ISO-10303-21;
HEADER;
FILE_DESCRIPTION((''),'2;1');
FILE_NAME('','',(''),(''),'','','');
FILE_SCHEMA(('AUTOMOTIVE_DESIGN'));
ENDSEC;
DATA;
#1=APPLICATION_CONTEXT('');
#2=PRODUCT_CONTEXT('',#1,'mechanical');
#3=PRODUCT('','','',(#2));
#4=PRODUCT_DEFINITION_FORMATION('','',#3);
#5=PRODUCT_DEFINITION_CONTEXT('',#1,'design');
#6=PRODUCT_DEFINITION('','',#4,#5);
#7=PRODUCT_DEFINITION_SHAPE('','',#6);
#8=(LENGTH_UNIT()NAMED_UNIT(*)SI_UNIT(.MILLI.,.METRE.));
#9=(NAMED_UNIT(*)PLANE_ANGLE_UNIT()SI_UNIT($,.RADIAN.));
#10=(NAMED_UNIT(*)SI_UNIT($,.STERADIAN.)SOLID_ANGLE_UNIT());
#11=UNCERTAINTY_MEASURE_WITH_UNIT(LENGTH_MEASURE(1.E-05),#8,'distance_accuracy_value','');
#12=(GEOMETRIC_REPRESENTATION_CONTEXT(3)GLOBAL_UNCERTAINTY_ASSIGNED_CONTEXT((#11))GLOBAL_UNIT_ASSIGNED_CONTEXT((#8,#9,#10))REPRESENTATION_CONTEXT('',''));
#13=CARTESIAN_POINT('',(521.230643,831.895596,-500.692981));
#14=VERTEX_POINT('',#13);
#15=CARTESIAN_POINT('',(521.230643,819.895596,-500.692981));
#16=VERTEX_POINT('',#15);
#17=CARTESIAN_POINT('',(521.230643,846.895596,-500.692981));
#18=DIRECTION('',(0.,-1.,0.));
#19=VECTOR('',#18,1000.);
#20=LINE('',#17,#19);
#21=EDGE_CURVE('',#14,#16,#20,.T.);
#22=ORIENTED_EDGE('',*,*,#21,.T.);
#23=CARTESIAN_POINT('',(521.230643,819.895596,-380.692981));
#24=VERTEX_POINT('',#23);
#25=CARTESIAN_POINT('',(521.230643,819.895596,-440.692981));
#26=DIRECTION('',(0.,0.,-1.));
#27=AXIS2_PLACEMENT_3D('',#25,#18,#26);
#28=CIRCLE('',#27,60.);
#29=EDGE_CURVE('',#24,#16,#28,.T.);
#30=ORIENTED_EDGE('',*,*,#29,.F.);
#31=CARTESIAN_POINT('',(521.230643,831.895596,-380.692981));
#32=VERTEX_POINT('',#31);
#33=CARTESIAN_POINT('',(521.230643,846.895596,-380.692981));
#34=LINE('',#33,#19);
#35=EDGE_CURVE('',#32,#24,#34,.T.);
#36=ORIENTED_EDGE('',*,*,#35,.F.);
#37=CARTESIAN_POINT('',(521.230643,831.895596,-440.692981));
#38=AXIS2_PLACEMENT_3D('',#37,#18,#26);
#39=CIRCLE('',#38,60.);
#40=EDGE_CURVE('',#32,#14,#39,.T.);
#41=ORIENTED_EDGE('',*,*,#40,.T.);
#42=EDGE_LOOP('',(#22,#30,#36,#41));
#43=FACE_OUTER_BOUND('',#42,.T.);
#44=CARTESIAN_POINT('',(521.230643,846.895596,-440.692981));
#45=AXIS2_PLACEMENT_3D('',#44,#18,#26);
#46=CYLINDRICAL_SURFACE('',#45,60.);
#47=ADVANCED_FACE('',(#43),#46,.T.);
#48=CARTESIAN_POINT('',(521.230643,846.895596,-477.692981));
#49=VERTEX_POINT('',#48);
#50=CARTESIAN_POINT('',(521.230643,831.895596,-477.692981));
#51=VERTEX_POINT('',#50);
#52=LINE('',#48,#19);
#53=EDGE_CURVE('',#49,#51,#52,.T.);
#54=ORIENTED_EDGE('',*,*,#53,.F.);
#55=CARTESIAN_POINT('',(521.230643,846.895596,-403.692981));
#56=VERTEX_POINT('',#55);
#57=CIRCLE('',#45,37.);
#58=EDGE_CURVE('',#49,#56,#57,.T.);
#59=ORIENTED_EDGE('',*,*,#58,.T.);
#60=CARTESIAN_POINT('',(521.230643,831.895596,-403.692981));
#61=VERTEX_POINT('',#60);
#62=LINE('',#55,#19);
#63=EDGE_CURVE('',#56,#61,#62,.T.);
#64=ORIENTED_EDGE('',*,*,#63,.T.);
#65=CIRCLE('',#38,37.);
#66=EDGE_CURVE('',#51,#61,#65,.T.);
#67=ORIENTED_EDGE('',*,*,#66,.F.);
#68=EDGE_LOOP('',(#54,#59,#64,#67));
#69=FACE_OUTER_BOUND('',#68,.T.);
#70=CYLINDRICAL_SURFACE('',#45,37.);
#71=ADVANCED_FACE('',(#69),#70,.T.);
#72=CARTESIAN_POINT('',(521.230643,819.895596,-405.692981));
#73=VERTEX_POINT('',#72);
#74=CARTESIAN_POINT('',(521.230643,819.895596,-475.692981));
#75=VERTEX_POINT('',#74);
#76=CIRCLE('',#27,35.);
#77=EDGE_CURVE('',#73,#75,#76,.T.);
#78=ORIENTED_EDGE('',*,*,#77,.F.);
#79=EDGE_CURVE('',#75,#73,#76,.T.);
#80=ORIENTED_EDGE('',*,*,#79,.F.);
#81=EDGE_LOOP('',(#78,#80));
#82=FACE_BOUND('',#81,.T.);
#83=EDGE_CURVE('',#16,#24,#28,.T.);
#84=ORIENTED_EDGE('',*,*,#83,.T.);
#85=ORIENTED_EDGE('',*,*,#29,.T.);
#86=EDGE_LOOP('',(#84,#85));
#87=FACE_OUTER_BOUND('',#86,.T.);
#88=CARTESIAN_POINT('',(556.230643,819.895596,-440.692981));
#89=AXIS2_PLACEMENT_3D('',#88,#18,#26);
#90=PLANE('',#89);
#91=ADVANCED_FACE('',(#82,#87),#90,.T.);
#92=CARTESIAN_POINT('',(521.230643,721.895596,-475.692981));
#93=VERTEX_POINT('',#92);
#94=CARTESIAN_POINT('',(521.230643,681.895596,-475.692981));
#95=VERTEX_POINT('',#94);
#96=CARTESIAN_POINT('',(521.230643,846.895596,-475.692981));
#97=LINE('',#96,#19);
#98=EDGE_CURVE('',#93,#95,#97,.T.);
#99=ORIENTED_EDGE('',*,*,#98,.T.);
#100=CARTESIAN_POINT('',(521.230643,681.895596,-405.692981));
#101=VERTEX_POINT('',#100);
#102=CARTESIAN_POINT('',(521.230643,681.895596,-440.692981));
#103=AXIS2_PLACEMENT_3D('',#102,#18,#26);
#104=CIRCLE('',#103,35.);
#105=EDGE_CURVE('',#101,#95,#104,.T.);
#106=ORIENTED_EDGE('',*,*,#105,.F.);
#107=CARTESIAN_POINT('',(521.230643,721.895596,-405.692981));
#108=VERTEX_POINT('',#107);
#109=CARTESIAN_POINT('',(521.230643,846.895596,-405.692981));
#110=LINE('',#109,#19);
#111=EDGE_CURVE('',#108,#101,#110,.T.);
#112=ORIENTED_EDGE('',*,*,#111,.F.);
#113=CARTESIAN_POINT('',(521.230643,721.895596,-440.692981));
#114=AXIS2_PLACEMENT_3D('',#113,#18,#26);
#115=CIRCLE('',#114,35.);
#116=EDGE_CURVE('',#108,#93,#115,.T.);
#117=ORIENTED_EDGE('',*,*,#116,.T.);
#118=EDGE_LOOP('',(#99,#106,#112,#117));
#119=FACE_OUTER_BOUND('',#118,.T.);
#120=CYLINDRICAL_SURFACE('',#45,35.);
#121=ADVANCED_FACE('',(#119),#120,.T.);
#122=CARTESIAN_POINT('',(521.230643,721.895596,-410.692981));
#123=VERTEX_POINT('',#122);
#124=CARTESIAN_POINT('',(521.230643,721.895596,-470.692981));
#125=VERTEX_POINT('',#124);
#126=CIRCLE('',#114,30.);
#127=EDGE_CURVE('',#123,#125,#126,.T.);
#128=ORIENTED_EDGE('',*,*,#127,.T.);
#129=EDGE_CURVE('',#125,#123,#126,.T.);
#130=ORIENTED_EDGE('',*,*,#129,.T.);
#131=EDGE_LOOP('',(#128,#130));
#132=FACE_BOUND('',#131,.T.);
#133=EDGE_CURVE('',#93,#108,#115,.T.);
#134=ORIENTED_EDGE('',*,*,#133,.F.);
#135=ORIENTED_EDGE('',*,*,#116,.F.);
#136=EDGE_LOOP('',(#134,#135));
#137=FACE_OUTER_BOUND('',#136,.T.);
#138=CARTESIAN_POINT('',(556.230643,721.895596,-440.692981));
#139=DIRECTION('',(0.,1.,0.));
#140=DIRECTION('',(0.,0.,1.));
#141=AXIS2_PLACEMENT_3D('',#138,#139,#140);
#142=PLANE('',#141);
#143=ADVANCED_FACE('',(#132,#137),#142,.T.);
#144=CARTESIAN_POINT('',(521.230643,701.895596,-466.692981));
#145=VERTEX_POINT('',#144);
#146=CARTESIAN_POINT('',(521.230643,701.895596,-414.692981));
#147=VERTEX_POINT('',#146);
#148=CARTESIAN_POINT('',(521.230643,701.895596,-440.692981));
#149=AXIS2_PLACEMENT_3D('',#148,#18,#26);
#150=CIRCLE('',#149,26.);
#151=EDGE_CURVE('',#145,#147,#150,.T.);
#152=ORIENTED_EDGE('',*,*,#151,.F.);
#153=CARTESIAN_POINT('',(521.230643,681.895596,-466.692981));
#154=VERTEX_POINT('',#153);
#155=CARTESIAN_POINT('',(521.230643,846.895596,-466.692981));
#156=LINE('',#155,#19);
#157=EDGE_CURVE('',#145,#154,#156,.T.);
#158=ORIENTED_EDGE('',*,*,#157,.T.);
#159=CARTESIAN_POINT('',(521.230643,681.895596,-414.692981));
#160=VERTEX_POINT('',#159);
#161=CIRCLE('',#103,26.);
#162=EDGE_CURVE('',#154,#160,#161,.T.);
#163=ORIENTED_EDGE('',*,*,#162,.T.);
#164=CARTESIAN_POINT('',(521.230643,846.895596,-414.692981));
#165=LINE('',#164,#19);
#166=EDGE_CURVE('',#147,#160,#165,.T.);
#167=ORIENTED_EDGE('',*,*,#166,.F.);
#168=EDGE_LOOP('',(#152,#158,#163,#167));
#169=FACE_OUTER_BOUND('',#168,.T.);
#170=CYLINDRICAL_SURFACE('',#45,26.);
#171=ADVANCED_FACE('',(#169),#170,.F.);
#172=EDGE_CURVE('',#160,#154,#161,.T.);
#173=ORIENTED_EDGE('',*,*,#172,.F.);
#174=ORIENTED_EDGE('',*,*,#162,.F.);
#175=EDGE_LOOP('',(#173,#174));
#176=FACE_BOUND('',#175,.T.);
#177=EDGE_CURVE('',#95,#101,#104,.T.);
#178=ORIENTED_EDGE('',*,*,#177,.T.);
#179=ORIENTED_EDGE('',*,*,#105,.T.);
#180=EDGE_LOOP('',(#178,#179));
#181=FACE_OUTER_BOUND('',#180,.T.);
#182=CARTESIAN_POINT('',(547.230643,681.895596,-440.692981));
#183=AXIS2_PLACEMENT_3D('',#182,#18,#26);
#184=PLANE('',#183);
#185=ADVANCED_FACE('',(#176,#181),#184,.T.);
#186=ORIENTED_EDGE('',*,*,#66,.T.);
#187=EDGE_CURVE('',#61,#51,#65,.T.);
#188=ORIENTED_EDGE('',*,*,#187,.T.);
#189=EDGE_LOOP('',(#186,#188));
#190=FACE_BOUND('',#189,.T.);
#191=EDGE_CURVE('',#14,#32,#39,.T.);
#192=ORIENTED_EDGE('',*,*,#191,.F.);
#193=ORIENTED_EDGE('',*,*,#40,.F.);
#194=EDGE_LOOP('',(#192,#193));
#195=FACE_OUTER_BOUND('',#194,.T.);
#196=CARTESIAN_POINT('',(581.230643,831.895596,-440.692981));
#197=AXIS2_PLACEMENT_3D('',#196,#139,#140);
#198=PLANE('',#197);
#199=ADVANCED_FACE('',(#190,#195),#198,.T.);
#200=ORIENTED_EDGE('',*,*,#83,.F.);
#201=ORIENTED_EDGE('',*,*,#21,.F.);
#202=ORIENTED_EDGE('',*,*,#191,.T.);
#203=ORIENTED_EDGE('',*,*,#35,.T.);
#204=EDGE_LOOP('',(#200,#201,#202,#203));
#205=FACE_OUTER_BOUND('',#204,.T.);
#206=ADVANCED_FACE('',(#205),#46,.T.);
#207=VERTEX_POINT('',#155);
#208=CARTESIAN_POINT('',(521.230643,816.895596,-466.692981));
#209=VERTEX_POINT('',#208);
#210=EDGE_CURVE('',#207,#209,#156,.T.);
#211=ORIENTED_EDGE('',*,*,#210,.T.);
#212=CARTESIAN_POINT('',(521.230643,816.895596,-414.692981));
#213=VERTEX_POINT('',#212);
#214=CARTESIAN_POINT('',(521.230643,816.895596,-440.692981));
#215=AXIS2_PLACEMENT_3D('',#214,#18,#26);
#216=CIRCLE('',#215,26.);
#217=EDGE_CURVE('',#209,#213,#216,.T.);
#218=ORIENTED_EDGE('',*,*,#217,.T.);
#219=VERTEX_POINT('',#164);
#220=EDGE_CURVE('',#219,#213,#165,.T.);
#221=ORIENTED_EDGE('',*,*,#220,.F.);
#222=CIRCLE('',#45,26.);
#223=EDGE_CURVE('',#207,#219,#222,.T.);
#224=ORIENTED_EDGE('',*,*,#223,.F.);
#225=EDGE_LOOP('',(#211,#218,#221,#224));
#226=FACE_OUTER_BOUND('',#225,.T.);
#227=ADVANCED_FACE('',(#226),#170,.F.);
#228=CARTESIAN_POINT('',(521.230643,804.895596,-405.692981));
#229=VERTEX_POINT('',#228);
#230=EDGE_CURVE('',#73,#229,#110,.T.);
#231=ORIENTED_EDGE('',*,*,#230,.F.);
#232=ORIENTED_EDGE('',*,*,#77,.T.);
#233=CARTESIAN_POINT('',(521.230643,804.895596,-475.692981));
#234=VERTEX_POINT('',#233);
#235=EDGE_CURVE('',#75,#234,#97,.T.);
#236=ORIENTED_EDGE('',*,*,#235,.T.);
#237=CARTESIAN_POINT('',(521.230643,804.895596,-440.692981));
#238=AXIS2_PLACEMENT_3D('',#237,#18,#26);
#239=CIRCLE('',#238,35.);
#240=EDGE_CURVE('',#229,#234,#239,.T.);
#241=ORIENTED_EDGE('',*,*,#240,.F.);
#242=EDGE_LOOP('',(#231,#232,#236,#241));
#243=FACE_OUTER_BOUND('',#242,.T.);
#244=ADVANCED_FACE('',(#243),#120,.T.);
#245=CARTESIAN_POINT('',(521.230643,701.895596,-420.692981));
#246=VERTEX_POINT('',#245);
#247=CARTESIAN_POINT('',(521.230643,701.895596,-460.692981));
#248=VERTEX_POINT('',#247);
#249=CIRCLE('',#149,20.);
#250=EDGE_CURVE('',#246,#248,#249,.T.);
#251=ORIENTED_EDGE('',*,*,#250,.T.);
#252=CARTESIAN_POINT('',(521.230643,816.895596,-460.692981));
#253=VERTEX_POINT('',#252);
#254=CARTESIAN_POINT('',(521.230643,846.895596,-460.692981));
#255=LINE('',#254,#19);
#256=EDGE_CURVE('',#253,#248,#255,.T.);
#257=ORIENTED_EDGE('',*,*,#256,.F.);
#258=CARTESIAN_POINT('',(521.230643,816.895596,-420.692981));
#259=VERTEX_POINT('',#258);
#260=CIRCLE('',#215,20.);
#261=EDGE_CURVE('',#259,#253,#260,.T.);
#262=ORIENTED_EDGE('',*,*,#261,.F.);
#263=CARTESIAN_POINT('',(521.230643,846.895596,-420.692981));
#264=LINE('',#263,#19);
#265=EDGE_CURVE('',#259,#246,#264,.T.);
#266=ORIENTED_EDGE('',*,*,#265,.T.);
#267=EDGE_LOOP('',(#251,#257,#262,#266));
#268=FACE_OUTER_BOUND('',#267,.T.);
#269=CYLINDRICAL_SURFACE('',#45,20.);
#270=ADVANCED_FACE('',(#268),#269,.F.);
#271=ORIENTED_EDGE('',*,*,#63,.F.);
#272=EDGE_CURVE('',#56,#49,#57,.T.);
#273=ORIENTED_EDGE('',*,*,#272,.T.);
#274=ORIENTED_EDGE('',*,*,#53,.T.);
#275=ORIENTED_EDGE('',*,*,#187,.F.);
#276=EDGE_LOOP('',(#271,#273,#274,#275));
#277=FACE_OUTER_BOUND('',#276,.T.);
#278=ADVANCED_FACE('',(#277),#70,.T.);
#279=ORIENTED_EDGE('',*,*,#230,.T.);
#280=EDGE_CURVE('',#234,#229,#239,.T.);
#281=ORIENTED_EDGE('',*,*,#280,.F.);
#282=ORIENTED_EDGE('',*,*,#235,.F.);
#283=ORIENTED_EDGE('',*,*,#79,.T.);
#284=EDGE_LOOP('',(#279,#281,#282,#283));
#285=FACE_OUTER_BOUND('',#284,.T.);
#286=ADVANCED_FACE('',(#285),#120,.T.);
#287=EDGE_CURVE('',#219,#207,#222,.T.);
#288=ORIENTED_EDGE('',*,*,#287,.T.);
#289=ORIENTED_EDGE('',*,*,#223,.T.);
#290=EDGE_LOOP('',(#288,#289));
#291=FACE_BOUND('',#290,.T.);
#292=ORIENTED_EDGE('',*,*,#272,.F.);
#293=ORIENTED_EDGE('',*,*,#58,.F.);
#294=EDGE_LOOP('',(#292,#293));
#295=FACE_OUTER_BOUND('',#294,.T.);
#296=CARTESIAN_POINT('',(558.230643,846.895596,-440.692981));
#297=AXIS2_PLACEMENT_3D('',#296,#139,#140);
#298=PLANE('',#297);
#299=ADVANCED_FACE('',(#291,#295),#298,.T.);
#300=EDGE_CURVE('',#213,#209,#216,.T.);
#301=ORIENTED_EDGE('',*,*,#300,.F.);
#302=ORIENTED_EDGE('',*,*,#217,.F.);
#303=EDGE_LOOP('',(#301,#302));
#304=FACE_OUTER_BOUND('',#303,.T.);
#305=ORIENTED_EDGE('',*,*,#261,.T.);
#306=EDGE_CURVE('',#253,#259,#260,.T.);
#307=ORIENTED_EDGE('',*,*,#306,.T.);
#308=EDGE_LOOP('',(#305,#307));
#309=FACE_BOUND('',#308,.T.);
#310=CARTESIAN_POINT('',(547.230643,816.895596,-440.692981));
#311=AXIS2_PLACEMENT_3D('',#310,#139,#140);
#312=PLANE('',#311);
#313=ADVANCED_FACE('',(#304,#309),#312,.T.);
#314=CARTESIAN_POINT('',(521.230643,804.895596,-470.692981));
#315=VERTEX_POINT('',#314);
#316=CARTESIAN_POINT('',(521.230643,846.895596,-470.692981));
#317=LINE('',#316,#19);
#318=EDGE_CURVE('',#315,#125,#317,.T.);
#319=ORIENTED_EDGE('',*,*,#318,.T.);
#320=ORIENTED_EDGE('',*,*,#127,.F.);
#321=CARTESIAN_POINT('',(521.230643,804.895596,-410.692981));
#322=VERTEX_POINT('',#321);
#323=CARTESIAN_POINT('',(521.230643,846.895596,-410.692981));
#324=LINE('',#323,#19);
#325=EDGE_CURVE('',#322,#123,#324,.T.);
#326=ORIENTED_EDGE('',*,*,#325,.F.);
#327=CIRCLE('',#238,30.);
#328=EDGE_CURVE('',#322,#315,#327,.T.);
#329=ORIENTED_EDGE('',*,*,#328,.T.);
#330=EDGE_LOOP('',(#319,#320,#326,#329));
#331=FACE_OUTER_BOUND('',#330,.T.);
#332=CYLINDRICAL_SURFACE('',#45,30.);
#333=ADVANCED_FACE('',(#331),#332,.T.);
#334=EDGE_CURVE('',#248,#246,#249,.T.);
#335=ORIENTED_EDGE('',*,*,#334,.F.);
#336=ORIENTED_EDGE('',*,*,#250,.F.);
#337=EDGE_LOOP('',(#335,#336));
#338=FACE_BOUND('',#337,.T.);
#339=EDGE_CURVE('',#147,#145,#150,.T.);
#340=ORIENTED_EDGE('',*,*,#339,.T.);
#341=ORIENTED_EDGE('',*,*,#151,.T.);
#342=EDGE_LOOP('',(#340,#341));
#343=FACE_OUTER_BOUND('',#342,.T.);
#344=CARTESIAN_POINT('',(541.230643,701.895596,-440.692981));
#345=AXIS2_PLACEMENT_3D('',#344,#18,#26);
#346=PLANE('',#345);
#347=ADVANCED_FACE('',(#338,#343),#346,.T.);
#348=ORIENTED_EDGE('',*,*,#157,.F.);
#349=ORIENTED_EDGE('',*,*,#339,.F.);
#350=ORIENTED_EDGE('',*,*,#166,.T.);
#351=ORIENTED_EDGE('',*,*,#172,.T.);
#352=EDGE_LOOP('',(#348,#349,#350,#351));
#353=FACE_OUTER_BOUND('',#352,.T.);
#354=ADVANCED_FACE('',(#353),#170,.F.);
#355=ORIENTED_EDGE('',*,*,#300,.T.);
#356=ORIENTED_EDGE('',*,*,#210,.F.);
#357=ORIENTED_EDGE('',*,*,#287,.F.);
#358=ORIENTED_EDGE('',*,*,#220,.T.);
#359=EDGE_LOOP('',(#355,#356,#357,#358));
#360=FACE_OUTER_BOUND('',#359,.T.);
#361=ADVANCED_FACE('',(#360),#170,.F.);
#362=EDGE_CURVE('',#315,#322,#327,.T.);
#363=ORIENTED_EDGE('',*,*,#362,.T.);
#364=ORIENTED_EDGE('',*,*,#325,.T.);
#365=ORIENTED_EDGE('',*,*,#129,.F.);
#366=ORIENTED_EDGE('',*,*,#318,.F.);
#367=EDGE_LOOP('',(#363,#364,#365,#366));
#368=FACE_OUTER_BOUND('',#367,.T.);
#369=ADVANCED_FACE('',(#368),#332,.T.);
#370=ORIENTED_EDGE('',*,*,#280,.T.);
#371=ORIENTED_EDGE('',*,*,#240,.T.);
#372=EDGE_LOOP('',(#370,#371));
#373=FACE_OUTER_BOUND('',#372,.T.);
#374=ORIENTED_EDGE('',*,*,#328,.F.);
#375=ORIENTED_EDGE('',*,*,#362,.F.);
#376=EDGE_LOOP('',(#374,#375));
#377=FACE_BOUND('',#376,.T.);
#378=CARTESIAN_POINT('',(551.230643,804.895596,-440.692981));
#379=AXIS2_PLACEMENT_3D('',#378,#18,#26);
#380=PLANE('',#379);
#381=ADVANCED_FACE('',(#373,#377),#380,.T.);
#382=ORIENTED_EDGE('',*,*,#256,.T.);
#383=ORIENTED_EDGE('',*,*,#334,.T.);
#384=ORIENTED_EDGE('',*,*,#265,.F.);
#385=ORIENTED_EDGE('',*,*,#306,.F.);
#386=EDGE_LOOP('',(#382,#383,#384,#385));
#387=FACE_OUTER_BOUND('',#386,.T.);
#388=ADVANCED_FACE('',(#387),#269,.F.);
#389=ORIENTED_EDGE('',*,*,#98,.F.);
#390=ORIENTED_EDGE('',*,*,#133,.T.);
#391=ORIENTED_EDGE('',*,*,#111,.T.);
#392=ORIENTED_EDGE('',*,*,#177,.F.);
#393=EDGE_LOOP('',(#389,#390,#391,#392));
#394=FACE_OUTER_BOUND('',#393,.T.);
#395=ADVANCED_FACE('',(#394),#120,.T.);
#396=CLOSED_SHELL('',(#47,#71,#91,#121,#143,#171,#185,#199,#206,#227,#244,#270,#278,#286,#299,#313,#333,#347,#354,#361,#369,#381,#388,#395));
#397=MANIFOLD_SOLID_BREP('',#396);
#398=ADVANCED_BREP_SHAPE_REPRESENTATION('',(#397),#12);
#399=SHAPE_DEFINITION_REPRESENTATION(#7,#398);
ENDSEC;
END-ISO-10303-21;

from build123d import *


with BuildPart() as part:
    # Sketch1 → Revolve1 (revolve)
    with BuildSketch(Plane.XY.offset(-440.692981355), mode=Mode.PRIVATE) as revolve1_sk:
        Polygon((551.230642584, 721.895595987), (551.230642584, 804.895595987), (556.230642584, 804.895595987), (556.230642584, 819.895595987), (581.230642584, 819.895595987), (581.230642584, 831.895595987), (558.230642584, 831.895595987), (558.230642584, 846.895595987), (547.230642584, 846.895595987), (547.230642584, 816.895595987), (541.230642584, 816.895595987), (541.230642584, 701.895595987), (547.230642584, 701.895595987), (547.230642584, 681.895595987), (556.230642584, 681.895595987), (556.230642584, 721.895595987), align=None)
    revolve(revolve1_sk.sketch.rotate(Axis((521.230642584, 846.895595987, -440.692981355), (0, -1, 0)), 270), axis=Axis((521.230642584, 846.895595987, -440.692981355), (0, -1, 0)))


solid = part.part
